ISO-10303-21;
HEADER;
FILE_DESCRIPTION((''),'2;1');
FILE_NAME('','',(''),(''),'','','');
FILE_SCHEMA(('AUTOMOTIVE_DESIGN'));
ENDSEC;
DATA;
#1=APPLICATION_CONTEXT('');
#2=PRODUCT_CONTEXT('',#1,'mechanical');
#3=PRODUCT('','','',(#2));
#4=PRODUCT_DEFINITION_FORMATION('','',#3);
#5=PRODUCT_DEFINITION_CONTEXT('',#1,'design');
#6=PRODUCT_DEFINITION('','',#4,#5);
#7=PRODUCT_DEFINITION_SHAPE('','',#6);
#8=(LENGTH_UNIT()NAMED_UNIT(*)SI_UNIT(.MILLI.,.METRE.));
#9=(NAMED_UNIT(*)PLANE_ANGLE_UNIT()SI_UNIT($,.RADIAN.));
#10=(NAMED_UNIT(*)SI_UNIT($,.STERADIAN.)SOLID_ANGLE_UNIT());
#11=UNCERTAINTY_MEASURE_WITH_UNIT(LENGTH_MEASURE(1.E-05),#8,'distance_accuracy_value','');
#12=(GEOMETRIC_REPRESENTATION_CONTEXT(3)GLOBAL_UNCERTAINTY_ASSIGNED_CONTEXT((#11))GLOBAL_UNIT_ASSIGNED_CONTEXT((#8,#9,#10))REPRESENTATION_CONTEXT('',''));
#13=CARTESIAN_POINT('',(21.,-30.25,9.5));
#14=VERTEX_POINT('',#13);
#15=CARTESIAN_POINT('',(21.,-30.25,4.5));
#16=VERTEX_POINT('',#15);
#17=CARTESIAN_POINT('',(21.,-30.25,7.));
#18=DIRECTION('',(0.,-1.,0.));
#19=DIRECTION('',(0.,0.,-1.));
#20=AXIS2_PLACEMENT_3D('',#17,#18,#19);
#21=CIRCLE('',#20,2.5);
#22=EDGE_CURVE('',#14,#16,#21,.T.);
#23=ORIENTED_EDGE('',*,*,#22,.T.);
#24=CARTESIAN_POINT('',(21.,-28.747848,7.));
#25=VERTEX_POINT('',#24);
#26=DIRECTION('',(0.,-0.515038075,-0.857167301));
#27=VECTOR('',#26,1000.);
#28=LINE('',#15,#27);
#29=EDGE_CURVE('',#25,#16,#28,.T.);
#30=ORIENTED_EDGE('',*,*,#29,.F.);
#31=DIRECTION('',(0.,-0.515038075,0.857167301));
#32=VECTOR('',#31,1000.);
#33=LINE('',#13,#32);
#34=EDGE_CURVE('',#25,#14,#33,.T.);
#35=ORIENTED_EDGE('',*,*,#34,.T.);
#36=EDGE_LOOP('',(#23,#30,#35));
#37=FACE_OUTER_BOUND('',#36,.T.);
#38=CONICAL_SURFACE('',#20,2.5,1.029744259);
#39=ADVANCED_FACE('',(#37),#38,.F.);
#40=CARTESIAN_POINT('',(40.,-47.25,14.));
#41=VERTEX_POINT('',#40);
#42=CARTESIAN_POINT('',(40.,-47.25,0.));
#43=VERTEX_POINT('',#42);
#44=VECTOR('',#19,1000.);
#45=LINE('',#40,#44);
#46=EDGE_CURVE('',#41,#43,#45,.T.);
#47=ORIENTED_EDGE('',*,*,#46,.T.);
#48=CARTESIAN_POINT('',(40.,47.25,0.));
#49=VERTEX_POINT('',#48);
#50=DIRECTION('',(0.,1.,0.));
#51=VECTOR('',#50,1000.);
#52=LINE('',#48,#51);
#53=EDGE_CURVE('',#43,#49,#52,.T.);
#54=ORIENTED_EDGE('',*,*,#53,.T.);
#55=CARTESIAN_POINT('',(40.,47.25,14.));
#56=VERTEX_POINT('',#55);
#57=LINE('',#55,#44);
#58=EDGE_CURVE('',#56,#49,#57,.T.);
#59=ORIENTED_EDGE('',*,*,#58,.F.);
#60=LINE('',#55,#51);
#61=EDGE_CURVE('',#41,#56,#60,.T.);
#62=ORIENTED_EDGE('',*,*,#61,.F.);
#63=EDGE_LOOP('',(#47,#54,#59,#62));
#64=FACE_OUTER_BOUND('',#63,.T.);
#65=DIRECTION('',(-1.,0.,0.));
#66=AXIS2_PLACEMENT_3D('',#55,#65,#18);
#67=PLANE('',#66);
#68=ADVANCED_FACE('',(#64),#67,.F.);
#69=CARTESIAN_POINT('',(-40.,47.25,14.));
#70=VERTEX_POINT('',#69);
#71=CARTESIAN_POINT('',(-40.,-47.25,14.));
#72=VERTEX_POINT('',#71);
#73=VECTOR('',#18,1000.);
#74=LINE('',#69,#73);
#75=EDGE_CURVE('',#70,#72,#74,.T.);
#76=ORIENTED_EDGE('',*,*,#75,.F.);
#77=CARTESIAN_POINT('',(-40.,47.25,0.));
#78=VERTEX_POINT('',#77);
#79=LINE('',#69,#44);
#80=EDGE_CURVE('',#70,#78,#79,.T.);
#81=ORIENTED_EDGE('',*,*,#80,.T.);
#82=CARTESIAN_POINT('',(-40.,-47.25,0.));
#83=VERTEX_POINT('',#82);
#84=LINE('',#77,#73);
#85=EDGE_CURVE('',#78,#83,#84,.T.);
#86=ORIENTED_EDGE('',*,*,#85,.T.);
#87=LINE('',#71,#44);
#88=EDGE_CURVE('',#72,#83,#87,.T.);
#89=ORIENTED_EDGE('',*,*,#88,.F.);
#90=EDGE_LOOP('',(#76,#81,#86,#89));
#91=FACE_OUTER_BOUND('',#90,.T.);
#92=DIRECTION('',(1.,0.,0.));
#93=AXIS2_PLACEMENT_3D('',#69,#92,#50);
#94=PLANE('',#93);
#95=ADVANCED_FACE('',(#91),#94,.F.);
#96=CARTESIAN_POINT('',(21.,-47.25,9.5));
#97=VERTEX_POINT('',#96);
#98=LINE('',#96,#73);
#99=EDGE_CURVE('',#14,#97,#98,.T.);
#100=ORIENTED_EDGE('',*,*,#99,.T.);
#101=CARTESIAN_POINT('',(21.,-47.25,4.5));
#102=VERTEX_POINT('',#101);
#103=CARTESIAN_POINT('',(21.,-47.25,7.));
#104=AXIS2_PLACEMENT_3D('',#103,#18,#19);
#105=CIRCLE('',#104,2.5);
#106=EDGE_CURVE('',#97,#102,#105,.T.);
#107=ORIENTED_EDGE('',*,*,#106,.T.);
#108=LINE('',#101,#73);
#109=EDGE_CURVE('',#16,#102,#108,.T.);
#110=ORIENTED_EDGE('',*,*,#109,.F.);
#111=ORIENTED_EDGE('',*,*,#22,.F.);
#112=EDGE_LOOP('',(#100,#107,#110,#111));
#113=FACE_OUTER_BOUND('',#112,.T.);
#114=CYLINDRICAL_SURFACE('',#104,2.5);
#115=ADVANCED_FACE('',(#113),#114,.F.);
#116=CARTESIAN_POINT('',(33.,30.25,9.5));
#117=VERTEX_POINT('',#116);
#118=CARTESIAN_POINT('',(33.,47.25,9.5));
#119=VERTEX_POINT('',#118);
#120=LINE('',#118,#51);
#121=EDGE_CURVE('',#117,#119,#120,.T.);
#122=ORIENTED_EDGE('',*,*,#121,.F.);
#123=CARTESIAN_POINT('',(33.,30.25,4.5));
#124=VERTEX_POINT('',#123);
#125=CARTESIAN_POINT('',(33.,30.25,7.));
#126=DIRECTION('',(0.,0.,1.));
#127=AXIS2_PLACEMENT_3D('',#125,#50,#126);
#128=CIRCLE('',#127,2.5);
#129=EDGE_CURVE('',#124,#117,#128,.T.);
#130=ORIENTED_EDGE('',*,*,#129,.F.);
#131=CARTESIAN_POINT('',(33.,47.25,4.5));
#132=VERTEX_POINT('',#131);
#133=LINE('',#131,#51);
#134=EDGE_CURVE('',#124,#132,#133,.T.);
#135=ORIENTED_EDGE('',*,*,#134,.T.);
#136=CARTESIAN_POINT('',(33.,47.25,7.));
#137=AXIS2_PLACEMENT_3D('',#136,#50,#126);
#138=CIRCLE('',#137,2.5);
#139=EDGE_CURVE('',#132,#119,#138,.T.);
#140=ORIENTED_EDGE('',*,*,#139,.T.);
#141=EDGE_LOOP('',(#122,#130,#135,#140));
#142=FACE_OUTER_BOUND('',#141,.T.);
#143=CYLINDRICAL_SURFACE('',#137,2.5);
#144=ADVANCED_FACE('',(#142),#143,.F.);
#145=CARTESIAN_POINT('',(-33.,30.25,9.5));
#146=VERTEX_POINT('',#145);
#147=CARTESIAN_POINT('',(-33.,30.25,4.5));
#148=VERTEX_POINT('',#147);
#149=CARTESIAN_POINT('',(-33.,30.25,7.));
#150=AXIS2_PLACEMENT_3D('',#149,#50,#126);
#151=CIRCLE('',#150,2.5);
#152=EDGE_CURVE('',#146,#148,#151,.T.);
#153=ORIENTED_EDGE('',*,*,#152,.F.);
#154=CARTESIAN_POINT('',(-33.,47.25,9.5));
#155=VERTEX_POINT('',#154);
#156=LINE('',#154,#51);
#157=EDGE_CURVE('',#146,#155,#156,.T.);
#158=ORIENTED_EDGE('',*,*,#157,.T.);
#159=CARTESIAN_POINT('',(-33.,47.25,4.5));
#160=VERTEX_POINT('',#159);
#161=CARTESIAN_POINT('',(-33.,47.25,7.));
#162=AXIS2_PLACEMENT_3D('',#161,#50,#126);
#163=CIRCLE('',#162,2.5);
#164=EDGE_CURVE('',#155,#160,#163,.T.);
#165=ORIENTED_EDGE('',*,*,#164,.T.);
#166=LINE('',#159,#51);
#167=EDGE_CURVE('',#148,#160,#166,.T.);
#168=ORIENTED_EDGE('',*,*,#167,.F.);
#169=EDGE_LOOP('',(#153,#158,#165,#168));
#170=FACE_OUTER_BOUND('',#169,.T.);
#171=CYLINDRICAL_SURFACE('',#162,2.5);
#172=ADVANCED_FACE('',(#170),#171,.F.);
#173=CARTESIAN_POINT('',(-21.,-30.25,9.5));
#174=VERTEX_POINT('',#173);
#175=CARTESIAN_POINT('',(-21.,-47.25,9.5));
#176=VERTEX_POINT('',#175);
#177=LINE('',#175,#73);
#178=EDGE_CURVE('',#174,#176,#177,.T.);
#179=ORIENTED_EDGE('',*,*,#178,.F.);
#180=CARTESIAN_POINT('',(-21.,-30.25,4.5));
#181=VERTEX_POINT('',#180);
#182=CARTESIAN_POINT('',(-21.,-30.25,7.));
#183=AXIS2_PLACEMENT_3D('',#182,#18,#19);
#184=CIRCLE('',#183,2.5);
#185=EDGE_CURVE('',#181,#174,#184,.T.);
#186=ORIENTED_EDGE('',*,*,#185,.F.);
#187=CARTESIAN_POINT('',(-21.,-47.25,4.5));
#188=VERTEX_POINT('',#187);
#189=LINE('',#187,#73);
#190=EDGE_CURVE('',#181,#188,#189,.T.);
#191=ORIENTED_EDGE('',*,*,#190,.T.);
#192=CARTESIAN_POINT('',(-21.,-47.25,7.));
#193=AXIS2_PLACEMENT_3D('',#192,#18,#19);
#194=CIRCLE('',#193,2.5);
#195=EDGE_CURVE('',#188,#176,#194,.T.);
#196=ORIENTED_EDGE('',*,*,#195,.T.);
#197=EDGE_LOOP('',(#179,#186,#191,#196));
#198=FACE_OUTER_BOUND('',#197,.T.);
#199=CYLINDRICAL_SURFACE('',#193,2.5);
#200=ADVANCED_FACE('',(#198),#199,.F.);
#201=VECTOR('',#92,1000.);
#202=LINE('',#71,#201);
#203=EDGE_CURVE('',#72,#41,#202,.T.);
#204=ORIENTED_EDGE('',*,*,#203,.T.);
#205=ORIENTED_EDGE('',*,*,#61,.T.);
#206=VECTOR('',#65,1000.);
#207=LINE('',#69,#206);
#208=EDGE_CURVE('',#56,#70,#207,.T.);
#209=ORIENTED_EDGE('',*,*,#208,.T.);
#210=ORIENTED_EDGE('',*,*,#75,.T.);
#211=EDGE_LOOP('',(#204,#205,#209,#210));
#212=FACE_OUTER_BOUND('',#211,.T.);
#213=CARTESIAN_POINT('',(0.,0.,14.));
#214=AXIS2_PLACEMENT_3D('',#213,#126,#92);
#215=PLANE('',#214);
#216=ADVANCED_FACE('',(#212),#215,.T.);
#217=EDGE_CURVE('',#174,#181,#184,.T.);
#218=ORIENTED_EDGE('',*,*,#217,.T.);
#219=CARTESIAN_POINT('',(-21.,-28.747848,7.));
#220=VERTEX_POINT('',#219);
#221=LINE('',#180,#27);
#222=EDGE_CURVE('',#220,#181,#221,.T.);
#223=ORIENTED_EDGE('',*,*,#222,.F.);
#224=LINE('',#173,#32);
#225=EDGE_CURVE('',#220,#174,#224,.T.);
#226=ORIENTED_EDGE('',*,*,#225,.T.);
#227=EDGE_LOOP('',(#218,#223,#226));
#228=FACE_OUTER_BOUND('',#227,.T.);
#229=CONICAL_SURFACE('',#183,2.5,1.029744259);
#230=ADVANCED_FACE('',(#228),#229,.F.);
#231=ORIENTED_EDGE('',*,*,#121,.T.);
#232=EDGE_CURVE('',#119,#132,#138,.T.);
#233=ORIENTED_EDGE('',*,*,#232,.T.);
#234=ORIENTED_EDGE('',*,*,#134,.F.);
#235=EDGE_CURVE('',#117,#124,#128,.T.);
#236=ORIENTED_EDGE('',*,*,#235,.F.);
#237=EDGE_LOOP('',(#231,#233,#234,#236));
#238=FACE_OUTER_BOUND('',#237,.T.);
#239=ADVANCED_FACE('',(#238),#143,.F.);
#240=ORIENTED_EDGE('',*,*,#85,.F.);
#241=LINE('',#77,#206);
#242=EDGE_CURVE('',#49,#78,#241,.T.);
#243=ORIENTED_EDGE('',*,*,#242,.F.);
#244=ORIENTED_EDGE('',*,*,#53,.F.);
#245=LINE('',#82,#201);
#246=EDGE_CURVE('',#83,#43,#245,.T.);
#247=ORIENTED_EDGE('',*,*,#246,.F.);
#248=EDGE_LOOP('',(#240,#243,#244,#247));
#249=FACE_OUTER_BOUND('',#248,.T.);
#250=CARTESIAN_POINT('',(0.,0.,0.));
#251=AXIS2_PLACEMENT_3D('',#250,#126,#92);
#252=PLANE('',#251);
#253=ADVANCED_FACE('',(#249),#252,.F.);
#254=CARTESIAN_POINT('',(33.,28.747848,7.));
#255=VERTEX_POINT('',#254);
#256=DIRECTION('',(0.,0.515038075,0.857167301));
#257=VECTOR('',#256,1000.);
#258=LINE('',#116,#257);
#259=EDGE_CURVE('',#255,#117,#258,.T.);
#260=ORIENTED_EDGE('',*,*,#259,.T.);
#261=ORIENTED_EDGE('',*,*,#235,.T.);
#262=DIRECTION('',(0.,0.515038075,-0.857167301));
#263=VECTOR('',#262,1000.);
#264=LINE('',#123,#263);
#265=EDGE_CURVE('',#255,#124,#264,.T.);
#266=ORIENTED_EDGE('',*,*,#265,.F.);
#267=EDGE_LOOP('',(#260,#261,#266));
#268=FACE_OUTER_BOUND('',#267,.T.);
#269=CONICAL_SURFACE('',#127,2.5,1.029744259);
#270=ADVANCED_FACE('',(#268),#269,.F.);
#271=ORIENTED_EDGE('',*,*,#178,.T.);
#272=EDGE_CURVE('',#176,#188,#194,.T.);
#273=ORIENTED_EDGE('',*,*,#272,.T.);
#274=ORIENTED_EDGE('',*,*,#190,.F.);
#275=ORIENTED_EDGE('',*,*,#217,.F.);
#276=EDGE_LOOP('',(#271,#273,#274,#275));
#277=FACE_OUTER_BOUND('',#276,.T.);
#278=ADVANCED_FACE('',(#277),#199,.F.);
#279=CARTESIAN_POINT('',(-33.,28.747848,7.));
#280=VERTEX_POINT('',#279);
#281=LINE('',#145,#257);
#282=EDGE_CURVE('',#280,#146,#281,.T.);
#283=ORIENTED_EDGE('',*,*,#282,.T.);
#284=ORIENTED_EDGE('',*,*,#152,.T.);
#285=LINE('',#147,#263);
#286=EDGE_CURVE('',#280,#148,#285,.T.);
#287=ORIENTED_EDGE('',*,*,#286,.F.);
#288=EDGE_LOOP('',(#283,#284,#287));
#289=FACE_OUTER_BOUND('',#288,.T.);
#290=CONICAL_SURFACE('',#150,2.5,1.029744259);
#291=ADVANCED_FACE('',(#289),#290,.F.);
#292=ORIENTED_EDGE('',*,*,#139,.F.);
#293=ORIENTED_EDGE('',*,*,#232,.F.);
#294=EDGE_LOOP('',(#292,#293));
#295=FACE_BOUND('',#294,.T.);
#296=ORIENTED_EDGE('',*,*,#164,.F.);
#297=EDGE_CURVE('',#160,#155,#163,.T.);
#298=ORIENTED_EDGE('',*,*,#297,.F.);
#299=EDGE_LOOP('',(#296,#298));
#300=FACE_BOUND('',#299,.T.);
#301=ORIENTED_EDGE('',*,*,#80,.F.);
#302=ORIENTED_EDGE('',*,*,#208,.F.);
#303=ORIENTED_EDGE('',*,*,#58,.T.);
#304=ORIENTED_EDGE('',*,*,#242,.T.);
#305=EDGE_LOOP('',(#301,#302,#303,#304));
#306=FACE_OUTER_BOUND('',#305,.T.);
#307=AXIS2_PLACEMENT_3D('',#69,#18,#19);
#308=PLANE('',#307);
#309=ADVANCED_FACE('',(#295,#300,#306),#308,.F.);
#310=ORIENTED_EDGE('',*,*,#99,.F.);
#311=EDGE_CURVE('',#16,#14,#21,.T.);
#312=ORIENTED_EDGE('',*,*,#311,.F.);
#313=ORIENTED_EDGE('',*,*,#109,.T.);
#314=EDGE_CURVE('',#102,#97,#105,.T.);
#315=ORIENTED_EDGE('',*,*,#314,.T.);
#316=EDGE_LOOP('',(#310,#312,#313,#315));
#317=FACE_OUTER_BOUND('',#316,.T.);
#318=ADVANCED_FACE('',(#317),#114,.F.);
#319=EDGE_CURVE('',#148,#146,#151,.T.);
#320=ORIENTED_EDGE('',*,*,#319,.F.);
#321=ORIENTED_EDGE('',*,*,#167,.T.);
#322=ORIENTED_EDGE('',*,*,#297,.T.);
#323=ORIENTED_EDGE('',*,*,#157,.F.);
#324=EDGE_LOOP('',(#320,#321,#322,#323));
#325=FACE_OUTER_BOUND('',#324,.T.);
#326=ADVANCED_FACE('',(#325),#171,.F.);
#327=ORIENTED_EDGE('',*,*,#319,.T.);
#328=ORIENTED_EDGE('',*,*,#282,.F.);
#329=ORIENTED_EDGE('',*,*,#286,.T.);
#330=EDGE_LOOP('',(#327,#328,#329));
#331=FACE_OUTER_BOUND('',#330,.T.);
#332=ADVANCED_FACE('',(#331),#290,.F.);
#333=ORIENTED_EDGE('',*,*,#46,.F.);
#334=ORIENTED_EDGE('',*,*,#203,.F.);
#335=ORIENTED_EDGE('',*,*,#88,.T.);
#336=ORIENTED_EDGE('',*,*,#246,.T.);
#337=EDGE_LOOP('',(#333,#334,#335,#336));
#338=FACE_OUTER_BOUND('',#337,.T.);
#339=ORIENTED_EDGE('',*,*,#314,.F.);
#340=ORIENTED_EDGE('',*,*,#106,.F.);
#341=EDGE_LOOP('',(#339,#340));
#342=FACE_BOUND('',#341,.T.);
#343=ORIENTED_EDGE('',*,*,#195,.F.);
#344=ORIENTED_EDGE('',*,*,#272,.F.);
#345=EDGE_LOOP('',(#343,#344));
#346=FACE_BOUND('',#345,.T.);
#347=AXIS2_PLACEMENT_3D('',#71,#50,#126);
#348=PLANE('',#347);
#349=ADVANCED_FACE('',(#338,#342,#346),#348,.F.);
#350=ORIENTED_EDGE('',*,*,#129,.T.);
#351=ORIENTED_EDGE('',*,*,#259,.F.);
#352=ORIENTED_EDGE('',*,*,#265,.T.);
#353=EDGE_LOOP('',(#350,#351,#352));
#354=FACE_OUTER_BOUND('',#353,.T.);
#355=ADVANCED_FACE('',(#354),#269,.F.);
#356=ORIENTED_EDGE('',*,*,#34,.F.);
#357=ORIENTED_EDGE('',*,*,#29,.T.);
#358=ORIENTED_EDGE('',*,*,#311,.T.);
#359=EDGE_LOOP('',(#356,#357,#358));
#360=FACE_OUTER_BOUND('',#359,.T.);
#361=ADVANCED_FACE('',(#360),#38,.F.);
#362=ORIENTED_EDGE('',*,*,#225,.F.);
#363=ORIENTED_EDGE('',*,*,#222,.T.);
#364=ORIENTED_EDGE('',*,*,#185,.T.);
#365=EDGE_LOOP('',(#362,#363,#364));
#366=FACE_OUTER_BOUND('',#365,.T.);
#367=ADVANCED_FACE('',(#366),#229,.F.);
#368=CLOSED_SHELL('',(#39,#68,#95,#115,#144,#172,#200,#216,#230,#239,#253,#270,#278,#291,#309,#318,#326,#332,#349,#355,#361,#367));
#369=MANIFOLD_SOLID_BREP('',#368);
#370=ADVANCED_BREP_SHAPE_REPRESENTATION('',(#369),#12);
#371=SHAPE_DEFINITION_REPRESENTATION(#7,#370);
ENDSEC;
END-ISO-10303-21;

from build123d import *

# Parameters (mm, degrees)
SKETCH_1_W             = 80
SKETCH_1_H             = 94.5
EXTRUDE_1_DEPTH        = 14
HOLE_WIZARD_M6_1_D     = 5
HOLE_WIZARD_M6_1_DEPTH = 17
HOLE_WIZARD_M6_1_TIP   = 1.502151548
HOLE_WIZARD_M6_2_D     = 5
HOLE_WIZARD_M6_2_DEPTH = 17
HOLE_WIZARD_M6_2_TIP   = 1.502151548


with BuildPart() as part:
    # 草图1 → 凸台-拉伸1 (new body)
    with BuildSketch(Plane.XY):
        Rectangle(SKETCH_1_W, SKETCH_1_H)
    extrude(amount=EXTRUDE_1_DEPTH)

    # M6 螺纹孔1
    with Locations(Plane(origin=(0, -47.25, 0), x_dir=(-1, 0, 0), z_dir=(0, -1, 0))):
        with Locations((-21, -7), (21, -7)):
            Hole(HOLE_WIZARD_M6_1_D / 2, depth=HOLE_WIZARD_M6_1_DEPTH)
            with Locations((0, 0, -(HOLE_WIZARD_M6_1_DEPTH + HOLE_WIZARD_M6_1_TIP / 2))):  # 118° drill point
                Cone(0, HOLE_WIZARD_M6_1_D / 2, HOLE_WIZARD_M6_1_TIP, mode=Mode.SUBTRACT)

    # M6 螺纹孔2
    with Locations(Plane(origin=(0, 47.25, 0), x_dir=(1, 0, 0), z_dir=(0, 1, 0))):
        with Locations((33, -7), (-33, -7)):
            Hole(HOLE_WIZARD_M6_2_D / 2, depth=HOLE_WIZARD_M6_2_DEPTH)
            with Locations((0, 0, -(HOLE_WIZARD_M6_2_DEPTH + HOLE_WIZARD_M6_2_TIP / 2))):  # 118° drill point
                Cone(0, HOLE_WIZARD_M6_2_D / 2, HOLE_WIZARD_M6_2_TIP, mode=Mode.SUBTRACT)


solid = part.part
